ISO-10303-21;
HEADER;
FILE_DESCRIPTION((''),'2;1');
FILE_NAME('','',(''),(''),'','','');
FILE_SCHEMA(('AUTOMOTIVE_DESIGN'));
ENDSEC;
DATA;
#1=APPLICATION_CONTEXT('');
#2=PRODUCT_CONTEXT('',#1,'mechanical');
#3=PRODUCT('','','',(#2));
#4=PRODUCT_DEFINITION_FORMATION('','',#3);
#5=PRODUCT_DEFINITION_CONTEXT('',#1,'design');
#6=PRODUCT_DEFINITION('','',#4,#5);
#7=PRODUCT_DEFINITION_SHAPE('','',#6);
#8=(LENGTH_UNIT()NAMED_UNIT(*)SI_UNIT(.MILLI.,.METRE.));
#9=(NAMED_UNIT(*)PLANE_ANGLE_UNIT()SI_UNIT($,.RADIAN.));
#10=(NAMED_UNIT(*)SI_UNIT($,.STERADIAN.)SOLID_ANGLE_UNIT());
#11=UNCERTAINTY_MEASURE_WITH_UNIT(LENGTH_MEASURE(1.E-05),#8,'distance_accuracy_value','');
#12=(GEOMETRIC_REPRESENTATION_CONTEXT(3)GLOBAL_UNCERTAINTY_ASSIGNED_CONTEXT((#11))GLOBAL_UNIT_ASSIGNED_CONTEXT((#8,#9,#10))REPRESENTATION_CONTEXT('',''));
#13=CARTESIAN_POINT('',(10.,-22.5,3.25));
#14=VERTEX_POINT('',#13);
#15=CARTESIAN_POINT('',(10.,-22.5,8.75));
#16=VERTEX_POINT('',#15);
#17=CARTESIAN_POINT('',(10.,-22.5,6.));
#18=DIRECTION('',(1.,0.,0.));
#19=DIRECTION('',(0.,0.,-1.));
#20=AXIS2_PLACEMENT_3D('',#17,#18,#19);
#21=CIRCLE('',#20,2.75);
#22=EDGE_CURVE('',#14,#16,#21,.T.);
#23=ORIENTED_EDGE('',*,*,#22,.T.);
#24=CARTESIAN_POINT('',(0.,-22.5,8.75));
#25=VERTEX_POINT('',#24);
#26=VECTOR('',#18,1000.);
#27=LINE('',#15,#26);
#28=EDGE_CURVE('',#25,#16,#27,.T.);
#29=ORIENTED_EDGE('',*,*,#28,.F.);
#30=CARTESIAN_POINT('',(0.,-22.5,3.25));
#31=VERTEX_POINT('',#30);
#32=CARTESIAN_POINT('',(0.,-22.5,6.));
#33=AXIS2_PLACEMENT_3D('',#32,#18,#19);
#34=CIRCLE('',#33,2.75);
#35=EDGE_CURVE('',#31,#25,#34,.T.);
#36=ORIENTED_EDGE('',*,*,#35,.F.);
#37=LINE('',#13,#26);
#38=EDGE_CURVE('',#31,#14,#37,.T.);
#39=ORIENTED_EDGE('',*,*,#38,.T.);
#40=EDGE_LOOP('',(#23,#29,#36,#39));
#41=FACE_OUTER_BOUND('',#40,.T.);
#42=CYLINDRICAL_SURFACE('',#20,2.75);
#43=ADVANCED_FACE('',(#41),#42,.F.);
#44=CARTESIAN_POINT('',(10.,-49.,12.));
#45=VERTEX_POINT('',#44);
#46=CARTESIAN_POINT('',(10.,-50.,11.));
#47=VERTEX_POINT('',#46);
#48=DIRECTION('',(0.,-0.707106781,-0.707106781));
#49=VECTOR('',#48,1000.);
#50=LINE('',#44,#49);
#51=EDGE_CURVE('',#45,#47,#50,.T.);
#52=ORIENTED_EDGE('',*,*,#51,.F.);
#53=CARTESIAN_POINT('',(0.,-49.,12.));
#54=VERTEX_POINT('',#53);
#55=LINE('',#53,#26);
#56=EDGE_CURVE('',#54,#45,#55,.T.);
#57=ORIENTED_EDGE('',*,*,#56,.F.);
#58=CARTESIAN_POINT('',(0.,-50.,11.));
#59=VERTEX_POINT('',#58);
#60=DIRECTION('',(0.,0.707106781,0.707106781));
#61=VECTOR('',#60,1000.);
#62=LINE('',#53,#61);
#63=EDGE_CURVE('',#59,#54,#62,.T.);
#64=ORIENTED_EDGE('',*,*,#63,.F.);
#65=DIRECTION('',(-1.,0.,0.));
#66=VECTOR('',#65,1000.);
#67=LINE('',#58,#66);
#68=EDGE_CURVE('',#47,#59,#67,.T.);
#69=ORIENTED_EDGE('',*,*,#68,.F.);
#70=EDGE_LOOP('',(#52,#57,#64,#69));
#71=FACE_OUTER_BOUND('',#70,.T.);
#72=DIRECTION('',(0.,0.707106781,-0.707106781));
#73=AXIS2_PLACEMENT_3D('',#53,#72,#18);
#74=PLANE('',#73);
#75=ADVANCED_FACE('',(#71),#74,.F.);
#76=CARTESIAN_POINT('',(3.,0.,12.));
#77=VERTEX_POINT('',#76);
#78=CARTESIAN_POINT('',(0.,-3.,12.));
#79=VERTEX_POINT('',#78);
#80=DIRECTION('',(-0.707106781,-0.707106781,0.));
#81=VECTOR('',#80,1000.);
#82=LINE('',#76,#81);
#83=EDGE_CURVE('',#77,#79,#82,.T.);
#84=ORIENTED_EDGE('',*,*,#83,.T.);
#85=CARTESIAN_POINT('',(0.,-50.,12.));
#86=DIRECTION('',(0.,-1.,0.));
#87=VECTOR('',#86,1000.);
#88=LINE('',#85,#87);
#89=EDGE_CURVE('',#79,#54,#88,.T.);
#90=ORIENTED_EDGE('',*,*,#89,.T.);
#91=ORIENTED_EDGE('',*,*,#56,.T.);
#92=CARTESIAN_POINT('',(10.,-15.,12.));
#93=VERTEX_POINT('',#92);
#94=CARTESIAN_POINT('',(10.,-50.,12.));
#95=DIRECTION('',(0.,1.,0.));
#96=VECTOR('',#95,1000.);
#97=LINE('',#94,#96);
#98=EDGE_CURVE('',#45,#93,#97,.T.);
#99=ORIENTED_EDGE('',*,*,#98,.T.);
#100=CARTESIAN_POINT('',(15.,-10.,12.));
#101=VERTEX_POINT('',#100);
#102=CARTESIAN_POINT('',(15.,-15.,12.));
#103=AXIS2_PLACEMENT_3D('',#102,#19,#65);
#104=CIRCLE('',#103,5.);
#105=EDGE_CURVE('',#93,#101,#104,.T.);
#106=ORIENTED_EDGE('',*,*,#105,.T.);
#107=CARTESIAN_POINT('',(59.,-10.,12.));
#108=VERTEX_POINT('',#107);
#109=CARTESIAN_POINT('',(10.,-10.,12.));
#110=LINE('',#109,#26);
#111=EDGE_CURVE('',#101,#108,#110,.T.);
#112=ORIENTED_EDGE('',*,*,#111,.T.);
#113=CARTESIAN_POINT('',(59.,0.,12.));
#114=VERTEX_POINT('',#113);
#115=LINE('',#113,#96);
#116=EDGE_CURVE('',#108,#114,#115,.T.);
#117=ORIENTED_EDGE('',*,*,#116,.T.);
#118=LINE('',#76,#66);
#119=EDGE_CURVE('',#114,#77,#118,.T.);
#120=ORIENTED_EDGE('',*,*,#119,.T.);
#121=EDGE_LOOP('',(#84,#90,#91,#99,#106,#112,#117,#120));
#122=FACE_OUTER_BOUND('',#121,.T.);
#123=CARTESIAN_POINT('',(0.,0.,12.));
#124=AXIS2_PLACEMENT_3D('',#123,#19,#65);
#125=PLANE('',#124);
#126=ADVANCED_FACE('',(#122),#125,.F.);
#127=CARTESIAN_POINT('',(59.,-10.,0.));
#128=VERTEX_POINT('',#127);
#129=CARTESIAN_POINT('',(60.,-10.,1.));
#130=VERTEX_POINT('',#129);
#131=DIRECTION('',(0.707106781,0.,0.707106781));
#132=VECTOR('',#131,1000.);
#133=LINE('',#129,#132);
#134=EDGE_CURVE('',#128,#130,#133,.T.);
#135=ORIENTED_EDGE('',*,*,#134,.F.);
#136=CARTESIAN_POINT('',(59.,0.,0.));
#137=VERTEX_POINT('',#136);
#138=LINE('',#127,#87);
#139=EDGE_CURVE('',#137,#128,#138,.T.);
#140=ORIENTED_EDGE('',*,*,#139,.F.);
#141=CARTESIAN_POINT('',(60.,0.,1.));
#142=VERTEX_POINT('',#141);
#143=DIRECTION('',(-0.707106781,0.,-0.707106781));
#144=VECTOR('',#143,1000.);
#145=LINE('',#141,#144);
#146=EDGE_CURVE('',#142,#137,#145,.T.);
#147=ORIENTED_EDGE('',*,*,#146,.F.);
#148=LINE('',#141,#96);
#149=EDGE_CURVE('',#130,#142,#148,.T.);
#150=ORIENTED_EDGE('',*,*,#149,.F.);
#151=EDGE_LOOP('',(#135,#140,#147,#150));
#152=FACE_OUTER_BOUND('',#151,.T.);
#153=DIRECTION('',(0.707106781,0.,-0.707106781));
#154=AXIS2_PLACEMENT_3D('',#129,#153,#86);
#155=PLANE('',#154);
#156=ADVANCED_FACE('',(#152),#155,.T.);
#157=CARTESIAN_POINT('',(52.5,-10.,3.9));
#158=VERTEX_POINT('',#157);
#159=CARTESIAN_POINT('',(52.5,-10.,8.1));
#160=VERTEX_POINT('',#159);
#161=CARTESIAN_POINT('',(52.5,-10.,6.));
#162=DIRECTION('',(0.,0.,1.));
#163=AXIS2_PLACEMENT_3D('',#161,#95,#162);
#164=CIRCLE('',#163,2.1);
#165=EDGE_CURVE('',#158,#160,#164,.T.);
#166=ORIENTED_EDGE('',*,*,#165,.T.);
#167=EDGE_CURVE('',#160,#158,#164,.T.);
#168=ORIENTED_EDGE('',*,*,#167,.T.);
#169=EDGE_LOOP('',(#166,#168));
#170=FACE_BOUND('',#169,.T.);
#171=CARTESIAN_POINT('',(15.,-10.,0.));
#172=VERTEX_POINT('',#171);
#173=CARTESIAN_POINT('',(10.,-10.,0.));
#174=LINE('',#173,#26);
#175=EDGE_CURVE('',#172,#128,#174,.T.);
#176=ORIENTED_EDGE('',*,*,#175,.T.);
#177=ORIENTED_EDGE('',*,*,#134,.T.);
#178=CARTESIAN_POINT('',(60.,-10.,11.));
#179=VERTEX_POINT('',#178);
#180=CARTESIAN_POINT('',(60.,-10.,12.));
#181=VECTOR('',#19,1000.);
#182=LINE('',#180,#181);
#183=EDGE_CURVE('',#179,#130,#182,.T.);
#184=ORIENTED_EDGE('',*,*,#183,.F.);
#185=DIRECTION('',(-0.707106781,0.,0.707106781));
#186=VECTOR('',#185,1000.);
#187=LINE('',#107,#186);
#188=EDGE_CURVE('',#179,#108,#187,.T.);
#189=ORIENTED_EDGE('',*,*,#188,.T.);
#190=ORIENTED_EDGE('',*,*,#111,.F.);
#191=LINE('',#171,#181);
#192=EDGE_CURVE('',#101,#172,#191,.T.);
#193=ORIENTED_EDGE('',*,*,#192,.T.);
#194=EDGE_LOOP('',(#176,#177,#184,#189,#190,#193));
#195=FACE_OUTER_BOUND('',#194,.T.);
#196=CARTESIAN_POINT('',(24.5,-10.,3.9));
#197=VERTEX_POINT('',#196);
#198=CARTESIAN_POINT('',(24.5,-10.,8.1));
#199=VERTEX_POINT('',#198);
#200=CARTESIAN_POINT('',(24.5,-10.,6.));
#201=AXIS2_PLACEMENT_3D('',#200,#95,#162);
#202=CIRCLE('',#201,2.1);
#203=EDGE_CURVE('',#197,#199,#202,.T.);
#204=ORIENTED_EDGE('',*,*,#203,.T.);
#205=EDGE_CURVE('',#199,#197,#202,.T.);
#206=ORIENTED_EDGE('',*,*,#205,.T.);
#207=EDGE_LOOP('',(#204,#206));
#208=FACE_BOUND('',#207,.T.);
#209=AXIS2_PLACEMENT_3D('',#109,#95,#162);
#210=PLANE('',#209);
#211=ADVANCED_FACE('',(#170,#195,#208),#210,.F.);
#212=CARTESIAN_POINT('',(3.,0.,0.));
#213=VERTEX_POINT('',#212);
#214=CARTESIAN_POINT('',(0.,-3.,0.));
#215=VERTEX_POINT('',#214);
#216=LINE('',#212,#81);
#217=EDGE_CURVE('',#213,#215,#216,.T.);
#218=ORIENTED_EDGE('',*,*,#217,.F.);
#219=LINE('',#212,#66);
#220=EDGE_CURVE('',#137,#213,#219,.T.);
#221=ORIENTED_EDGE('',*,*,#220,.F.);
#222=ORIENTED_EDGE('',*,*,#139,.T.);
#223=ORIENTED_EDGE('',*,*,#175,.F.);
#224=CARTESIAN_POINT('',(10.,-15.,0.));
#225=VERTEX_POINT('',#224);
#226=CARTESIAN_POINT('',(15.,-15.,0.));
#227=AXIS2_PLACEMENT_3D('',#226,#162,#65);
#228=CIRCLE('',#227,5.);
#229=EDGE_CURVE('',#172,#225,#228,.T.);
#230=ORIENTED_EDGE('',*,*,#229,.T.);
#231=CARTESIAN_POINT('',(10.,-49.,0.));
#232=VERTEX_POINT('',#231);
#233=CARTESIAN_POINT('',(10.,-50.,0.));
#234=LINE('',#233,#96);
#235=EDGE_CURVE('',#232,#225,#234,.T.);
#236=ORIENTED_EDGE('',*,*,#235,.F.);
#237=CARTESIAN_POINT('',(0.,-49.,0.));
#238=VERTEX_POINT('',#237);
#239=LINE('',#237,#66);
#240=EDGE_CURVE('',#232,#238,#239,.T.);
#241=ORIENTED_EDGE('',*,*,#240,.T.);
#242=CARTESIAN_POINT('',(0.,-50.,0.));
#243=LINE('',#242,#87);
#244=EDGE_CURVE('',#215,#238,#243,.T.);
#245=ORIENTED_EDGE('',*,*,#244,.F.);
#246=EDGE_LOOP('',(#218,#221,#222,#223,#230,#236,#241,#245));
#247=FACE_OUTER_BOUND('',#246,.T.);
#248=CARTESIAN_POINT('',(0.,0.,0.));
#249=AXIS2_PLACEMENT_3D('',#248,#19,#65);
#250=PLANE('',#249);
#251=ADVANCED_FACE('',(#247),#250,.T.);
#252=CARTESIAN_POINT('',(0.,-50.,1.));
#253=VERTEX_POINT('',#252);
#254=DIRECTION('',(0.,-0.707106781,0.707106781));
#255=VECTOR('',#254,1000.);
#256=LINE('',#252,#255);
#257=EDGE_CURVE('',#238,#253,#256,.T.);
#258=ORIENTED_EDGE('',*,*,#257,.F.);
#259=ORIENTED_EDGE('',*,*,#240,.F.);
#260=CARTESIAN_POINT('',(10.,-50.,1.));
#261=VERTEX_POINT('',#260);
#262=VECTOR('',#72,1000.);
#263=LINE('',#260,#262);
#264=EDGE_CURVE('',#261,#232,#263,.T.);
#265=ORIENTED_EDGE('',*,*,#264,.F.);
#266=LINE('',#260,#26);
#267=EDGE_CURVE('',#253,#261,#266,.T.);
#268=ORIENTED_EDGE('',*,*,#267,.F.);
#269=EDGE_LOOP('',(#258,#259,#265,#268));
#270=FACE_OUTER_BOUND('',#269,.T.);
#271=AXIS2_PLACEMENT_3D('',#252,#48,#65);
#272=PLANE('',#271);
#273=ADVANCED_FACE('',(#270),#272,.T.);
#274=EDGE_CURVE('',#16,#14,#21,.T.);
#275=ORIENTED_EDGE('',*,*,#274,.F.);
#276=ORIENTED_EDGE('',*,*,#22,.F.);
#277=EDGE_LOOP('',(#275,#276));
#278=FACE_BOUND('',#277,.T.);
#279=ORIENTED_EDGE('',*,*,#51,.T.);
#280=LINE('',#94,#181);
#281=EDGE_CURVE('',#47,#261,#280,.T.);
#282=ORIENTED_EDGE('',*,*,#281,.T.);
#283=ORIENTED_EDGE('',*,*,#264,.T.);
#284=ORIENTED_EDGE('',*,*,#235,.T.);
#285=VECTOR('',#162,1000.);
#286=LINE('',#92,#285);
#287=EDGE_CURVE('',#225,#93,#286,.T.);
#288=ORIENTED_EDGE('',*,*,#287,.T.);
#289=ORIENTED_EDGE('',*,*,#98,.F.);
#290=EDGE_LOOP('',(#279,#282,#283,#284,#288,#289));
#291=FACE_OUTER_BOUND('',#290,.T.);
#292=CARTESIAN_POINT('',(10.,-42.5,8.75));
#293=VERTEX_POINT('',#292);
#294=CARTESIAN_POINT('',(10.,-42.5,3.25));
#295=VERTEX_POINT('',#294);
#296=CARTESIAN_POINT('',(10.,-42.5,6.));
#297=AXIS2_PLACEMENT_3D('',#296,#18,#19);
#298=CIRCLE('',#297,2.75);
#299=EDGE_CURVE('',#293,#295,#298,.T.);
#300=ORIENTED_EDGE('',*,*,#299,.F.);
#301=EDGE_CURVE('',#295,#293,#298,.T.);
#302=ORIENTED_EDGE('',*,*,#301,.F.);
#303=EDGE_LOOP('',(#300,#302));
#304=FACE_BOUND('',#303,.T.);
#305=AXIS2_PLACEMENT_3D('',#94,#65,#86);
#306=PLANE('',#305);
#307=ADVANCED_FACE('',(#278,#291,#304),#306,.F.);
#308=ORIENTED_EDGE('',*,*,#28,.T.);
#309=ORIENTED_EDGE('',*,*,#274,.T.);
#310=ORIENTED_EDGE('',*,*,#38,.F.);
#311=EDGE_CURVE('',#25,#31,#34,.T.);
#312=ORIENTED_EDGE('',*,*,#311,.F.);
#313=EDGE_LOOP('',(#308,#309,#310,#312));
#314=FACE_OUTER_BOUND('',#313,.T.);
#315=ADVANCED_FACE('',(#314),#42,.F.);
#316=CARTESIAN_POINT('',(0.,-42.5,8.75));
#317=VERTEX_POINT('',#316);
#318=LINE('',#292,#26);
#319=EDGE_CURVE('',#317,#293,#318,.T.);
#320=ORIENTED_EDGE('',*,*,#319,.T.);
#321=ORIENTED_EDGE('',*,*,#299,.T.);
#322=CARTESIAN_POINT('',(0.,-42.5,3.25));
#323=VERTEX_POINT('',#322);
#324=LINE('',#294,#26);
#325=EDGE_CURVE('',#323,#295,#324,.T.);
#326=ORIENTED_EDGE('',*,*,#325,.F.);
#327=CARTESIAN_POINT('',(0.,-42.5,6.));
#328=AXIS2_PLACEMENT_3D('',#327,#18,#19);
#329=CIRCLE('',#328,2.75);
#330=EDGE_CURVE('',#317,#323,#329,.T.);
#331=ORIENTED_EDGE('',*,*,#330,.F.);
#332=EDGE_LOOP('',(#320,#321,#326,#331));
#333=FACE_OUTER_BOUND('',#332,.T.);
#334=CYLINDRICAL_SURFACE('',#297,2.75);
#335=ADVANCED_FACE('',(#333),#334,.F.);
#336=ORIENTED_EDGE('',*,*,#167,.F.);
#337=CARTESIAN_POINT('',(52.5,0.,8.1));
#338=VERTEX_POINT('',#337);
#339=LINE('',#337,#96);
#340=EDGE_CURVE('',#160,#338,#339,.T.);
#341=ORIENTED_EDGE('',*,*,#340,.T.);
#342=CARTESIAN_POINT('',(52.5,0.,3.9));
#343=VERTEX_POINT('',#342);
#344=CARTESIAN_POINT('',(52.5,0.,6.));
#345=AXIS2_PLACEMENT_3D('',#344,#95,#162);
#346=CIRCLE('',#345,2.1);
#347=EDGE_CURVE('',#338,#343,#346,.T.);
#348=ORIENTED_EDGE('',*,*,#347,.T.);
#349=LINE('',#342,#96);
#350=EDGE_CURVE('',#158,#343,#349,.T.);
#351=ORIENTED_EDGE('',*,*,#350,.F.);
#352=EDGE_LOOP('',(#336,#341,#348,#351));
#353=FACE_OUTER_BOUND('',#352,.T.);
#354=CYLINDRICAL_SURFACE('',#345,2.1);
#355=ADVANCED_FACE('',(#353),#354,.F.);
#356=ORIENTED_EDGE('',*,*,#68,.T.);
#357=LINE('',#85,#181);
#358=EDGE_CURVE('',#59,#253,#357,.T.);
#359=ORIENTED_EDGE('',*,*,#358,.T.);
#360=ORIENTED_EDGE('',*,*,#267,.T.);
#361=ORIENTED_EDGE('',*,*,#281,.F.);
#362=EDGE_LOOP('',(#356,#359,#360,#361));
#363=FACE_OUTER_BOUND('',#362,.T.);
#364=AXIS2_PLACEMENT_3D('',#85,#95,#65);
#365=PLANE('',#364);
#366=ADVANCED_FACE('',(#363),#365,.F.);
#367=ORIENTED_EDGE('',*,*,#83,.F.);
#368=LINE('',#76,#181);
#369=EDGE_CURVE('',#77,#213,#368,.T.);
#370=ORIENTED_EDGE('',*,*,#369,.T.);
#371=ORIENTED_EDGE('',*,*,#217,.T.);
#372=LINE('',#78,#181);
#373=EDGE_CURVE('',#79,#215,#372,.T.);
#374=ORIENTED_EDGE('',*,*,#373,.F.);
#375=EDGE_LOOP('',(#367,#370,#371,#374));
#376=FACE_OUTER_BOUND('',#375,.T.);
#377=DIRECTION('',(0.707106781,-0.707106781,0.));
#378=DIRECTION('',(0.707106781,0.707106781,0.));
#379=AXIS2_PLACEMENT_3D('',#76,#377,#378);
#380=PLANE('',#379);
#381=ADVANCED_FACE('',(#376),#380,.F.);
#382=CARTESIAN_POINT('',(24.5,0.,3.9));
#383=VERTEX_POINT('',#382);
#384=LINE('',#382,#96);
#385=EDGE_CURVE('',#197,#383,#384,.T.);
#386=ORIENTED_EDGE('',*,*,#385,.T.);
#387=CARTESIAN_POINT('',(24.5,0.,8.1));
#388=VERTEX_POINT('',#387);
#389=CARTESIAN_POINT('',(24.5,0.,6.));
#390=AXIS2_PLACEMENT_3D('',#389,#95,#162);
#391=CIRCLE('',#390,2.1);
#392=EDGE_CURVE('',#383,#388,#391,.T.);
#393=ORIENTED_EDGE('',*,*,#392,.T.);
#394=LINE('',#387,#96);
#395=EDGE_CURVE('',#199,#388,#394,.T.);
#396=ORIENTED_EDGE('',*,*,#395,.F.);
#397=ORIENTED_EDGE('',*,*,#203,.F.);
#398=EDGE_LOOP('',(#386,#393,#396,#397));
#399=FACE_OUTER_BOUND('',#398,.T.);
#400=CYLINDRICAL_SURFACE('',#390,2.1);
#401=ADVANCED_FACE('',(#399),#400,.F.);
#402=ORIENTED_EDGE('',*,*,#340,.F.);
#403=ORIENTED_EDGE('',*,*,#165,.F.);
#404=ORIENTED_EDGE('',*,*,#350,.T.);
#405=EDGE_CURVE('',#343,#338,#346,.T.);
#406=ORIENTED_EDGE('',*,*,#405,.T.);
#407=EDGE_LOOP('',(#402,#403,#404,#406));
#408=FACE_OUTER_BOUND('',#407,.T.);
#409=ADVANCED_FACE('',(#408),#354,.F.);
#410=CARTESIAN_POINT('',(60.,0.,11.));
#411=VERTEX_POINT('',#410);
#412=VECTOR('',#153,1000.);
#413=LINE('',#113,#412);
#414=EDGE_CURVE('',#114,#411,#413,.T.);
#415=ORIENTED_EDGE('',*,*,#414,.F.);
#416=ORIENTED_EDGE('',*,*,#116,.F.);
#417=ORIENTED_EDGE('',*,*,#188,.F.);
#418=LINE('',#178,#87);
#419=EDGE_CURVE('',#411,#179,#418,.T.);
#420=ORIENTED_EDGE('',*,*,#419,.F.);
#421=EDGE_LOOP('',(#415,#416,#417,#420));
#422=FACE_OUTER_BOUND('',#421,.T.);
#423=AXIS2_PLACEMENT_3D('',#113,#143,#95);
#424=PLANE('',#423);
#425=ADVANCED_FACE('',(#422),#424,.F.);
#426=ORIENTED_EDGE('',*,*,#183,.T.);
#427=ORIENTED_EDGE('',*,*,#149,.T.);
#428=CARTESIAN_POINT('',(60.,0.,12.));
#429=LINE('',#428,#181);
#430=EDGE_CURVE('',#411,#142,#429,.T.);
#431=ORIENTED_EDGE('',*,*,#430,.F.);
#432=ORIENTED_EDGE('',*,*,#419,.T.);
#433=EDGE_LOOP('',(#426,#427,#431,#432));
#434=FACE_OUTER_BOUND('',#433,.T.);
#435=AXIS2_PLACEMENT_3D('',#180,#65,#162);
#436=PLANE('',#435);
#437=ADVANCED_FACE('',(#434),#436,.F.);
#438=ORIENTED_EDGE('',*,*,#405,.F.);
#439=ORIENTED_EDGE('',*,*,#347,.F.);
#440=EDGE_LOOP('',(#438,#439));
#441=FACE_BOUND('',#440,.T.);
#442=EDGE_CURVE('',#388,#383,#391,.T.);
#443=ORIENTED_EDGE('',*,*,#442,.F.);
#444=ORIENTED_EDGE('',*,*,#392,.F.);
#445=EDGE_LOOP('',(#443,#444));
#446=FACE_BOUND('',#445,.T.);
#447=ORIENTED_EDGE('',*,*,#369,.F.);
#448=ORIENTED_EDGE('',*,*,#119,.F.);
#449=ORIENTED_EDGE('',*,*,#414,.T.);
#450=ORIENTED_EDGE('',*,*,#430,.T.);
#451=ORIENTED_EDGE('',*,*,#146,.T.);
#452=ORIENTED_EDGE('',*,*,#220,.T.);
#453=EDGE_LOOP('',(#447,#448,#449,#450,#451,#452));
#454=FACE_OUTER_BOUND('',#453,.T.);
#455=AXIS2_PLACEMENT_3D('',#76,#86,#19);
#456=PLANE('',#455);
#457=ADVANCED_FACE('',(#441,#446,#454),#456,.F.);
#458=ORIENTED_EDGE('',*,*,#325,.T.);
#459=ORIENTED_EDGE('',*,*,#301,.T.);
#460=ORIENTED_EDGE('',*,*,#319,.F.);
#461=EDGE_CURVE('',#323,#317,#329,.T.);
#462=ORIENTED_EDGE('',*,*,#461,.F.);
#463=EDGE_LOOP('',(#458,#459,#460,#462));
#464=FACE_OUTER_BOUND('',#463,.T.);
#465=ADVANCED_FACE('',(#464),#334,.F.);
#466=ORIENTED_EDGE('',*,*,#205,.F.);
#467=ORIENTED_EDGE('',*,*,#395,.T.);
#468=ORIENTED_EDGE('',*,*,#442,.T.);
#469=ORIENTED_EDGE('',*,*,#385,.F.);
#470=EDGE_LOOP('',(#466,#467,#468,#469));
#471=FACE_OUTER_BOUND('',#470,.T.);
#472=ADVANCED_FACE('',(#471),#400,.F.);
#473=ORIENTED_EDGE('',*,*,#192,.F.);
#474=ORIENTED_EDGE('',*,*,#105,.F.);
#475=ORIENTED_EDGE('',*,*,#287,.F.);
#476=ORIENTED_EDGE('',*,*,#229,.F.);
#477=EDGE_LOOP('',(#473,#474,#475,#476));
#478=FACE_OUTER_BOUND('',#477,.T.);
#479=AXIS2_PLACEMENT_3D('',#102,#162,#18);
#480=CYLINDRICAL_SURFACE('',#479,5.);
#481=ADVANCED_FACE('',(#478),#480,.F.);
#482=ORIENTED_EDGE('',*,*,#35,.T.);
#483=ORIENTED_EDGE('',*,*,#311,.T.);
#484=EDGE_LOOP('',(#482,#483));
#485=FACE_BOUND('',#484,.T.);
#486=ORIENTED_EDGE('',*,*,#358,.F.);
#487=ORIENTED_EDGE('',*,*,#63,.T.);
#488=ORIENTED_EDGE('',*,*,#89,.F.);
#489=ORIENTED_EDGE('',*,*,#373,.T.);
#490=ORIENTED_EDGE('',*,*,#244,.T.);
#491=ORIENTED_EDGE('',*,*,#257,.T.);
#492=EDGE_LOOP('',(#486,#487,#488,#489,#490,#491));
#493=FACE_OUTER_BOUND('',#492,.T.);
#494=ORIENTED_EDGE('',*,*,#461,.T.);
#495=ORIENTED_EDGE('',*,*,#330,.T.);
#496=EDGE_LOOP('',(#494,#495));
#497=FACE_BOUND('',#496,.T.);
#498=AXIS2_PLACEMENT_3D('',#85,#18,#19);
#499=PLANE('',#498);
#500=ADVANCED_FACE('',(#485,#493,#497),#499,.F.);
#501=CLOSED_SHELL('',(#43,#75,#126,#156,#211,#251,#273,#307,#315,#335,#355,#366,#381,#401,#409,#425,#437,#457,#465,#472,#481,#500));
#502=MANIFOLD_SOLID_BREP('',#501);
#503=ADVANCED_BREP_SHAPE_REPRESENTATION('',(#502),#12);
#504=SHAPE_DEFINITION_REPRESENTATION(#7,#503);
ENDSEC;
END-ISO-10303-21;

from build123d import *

# Parameters (mm, degrees)
BOSS_EXTRUDE1_DEPTH   = 12
M5_TAPPED_HOLE1_D     = 4.2
M5_TAPPED_HOLE1_DEPTH = 12.4
M5_TAPPED_HOLE1_TIP   = 1.2618073
M5_CLEARANCE_HOLE1_D  = 5.5
CHAMFER2_SIZE         = 1
FILLET1_R             = 5


with BuildPart() as part:
    # Sketch1 → Boss-Extrude1 (new body)
    with BuildSketch(Plane.XY):
        Polygon((3, 0), (60, 0), (60, -10), (10, -10), (10, -50), (0, -50), (0, -3), align=None)
    extrude(amount=BOSS_EXTRUDE1_DEPTH)

    # M5 Tapped Hole1
    with Locations(Plane(origin=(0, 0, 0), x_dir=(-1, 0, 0), z_dir=(0, 1, 0))):
        with Locations((-52.5, 6), (-24.5, 6)):
            Hole(M5_TAPPED_HOLE1_D / 2, depth=M5_TAPPED_HOLE1_DEPTH)
            with Locations((0, 0, -(M5_TAPPED_HOLE1_DEPTH + M5_TAPPED_HOLE1_TIP / 2))):  # 118° drill point
                Cone(0, M5_TAPPED_HOLE1_D / 2, M5_TAPPED_HOLE1_TIP, mode=Mode.SUBTRACT)

    # M5 Clearance Hole1 (through all)
    with Locations(Plane(origin=(10, 0, 0), x_dir=(0, 0, -1), z_dir=(1, 0, 0))):
        with Locations((-6, -42.5), (-6, -22.5)):
            Hole(M5_CLEARANCE_HOLE1_D / 2)

    # Chamfer2
    chamfer2_edges = [part.edges().sort_by_distance(p)[0] for p in [
        (60, -5, 0),
        (5, -50, 12),
        (60, -5, 12),
        (5, -50, 0),
    ]]
    chamfer(chamfer2_edges, length=CHAMFER2_SIZE)

    # Fillet1
    fillet1_edges = [part.edges().sort_by_distance(p)[0] for p in [
        (10, -10, 6),
    ]]
    fillet(fillet1_edges, radius=FILLET1_R)


solid = part.part
